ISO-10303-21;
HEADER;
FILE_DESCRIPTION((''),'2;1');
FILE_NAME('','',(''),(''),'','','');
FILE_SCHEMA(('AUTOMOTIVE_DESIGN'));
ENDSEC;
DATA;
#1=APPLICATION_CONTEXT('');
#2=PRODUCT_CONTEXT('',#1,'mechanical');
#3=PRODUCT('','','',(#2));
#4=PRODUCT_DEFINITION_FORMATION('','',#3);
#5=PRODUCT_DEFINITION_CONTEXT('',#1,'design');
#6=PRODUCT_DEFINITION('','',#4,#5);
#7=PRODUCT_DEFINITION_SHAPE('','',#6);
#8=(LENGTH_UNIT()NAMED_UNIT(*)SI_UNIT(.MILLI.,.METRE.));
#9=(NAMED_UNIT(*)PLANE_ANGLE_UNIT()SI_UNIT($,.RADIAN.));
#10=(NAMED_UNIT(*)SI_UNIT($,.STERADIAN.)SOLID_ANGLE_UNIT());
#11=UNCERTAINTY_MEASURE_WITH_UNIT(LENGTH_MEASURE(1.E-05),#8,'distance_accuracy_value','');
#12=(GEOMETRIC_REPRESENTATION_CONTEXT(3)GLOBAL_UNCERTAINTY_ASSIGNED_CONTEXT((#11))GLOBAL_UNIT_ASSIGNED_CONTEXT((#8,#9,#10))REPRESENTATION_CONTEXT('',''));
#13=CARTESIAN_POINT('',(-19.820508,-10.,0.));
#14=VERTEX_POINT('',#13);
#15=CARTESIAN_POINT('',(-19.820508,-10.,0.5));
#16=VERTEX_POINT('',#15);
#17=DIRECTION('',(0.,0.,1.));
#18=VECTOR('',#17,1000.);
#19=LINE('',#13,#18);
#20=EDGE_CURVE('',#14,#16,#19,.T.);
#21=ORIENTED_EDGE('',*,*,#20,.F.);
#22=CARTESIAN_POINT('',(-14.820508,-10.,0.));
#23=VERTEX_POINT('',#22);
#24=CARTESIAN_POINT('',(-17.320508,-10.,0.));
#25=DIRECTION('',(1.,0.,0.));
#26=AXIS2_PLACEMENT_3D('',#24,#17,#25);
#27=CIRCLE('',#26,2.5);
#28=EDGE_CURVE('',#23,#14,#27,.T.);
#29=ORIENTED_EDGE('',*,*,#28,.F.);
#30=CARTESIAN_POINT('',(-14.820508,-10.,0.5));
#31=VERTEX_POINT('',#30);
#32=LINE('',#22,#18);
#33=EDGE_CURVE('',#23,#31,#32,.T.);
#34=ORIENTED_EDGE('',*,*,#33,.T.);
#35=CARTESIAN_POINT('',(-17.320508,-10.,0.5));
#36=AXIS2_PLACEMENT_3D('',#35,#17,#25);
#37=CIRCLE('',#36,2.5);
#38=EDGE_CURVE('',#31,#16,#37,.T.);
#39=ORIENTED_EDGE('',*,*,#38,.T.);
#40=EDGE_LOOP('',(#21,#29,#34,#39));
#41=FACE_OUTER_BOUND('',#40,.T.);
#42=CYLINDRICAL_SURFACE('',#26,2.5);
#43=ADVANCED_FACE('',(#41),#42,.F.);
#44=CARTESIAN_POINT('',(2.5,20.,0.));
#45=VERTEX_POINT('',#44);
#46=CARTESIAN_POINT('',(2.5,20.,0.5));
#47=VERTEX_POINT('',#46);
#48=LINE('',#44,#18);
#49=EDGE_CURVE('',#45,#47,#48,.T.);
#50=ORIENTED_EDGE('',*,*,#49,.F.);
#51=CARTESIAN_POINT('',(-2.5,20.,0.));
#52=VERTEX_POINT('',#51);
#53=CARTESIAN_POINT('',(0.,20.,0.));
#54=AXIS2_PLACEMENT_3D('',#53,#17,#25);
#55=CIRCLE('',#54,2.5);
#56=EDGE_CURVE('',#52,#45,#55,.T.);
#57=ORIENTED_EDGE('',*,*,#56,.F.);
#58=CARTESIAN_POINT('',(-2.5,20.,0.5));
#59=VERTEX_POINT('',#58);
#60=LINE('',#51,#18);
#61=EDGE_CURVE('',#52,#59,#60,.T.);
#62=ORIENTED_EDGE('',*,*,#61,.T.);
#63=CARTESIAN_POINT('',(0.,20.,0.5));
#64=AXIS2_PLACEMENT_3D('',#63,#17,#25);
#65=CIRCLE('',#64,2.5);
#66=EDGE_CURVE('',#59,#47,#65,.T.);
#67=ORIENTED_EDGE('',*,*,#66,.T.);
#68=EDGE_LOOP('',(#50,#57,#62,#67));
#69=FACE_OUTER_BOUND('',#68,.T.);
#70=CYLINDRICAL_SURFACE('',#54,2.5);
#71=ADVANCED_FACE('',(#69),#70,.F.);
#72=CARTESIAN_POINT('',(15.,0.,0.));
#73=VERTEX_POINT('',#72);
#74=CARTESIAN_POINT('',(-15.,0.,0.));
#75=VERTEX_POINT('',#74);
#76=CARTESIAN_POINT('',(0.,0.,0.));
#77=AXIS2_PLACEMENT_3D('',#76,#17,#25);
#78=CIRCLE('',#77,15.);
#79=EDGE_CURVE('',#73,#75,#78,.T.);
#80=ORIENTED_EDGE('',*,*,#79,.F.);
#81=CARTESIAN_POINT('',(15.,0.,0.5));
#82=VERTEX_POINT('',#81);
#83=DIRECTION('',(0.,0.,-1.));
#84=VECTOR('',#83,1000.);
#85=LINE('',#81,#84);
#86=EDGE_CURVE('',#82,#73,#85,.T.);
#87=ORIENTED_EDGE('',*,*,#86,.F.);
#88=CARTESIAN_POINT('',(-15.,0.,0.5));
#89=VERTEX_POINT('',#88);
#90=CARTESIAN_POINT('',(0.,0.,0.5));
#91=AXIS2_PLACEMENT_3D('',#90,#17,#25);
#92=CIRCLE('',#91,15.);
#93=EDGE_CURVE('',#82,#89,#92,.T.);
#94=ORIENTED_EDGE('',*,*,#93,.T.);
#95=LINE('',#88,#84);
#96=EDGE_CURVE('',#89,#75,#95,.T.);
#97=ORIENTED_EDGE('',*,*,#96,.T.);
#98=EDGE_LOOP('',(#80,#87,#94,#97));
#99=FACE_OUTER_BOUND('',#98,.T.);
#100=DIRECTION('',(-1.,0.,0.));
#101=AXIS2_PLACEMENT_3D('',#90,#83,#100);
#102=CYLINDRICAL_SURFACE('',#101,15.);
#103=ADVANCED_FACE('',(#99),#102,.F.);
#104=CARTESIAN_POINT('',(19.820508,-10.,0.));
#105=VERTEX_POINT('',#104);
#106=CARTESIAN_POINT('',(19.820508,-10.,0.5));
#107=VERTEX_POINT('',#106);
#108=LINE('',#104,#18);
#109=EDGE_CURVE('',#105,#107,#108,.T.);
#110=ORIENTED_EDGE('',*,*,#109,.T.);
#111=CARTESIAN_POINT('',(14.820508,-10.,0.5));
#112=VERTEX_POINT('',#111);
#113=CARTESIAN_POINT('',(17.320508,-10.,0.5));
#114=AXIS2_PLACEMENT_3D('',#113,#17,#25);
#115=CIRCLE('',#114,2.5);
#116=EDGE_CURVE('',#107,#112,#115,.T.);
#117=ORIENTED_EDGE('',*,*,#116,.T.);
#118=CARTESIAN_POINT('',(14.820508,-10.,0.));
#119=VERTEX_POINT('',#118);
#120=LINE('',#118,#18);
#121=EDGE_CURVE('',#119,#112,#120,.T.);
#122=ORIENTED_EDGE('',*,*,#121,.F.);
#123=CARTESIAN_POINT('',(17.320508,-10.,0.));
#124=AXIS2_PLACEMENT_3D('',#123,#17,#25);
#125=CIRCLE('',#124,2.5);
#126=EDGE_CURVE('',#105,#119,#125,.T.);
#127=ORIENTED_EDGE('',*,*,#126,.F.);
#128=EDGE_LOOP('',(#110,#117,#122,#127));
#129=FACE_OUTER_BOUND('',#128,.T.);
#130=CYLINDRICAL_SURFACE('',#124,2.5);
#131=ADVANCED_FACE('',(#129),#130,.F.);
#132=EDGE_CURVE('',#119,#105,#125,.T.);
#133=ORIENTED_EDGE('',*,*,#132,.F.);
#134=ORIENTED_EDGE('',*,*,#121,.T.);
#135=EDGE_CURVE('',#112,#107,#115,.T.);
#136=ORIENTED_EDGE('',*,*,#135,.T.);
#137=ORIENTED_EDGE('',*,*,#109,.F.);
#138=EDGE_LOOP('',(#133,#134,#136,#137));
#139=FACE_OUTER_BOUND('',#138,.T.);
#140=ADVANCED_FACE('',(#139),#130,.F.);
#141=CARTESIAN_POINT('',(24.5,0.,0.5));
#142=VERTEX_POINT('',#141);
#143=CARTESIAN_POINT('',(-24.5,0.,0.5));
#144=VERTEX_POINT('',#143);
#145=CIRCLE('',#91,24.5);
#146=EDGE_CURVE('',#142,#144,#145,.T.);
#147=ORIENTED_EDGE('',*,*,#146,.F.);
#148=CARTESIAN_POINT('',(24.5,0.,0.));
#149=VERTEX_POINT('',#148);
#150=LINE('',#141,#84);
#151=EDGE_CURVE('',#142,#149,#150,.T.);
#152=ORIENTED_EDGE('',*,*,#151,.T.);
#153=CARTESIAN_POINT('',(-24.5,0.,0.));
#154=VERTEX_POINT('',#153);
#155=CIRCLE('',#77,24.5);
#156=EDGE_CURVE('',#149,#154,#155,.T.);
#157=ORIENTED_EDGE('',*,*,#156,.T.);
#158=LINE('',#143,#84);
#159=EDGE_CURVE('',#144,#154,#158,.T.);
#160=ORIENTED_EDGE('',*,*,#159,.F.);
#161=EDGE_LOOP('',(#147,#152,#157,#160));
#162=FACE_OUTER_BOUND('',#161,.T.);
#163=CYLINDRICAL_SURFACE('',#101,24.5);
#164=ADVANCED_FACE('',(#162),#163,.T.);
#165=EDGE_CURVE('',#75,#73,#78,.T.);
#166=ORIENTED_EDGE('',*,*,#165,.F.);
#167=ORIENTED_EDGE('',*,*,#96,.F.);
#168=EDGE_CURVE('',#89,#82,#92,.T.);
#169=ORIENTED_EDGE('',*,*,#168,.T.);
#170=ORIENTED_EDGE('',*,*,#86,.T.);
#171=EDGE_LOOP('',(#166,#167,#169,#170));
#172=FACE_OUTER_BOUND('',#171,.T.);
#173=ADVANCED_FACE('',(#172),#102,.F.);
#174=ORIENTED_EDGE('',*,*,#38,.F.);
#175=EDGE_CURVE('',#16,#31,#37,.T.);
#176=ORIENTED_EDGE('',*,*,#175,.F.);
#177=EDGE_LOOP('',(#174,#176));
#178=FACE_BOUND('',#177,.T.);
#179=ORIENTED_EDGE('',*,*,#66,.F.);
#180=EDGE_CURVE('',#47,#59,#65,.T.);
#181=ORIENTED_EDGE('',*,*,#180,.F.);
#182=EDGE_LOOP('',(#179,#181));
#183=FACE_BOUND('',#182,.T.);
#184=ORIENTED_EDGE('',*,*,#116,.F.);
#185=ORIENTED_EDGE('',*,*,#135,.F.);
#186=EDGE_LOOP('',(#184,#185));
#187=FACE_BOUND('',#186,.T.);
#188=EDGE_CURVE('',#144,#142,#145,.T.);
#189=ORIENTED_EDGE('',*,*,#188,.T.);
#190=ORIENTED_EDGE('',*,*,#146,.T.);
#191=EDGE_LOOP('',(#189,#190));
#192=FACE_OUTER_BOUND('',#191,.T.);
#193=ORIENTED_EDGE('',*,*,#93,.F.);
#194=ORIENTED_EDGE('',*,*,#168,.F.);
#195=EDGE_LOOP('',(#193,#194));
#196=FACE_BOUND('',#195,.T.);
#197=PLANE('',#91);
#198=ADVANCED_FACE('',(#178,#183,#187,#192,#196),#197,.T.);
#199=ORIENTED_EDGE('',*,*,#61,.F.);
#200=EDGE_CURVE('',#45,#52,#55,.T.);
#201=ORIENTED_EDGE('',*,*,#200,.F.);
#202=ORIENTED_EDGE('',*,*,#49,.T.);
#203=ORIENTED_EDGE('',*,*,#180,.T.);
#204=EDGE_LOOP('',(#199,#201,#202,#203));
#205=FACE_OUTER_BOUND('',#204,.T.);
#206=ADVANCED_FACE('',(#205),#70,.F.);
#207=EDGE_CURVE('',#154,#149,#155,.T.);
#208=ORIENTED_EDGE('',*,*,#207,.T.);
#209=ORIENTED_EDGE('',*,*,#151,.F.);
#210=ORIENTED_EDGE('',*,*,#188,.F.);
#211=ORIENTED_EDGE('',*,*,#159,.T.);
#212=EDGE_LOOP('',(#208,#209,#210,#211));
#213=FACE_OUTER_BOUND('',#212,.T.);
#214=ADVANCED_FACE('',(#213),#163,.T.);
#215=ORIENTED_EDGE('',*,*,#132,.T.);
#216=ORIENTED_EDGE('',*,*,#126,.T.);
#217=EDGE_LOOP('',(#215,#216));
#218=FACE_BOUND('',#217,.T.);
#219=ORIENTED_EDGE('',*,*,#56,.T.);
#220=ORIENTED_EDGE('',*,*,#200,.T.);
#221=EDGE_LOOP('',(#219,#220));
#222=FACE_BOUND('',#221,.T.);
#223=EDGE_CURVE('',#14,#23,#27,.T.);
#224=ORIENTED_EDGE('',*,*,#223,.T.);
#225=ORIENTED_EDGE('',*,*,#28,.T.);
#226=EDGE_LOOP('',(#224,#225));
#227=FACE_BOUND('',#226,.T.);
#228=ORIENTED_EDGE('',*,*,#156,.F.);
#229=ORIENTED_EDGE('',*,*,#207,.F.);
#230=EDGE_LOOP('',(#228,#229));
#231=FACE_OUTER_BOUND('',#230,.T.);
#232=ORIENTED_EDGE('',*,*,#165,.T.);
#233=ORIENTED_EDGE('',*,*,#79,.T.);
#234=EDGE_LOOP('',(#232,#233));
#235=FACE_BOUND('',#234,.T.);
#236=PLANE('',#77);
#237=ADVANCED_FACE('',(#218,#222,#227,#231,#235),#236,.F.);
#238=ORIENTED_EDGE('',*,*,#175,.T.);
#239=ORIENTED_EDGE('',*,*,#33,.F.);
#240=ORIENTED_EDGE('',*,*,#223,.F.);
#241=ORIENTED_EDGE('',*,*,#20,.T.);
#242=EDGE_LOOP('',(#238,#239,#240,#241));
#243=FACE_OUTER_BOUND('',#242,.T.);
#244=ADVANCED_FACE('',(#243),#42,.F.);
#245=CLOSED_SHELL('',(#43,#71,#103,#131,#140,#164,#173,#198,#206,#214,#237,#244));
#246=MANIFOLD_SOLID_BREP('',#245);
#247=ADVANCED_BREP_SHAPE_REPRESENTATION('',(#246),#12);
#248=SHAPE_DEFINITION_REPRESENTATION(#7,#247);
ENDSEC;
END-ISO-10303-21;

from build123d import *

# Parameters (mm, degrees)
SKETCH1_R           = 24.5
SKETCH1_R_2         = 15
BOSS_EXTRUDE1_DEPTH = 0.5
SKETCH2_R           = 2.5
CUT_EXTRUDE1_DEPTH  = 0.5


with BuildPart() as part:
    # Sketch1 → Boss-Extrude1 (new body)
    with BuildSketch(Plane.XY):
        Circle(SKETCH1_R)
        Circle(SKETCH1_R_2, mode=Mode.SUBTRACT)
    extrude(amount=BOSS_EXTRUDE1_DEPTH)

    # Sketch2 → Cut-Extrude1 (cut)
    with BuildSketch(Plane.XY.offset(0.5)):
        with Locations((0, 20)):
            Circle(SKETCH2_R)
        with Locations((17.320508076, -10)):
            Circle(SKETCH2_R)
        with Locations((-17.320508076, -10)):
            Circle(SKETCH2_R)
    extrude(amount=-CUT_EXTRUDE1_DEPTH, mode=Mode.SUBTRACT)


solid = part.part
